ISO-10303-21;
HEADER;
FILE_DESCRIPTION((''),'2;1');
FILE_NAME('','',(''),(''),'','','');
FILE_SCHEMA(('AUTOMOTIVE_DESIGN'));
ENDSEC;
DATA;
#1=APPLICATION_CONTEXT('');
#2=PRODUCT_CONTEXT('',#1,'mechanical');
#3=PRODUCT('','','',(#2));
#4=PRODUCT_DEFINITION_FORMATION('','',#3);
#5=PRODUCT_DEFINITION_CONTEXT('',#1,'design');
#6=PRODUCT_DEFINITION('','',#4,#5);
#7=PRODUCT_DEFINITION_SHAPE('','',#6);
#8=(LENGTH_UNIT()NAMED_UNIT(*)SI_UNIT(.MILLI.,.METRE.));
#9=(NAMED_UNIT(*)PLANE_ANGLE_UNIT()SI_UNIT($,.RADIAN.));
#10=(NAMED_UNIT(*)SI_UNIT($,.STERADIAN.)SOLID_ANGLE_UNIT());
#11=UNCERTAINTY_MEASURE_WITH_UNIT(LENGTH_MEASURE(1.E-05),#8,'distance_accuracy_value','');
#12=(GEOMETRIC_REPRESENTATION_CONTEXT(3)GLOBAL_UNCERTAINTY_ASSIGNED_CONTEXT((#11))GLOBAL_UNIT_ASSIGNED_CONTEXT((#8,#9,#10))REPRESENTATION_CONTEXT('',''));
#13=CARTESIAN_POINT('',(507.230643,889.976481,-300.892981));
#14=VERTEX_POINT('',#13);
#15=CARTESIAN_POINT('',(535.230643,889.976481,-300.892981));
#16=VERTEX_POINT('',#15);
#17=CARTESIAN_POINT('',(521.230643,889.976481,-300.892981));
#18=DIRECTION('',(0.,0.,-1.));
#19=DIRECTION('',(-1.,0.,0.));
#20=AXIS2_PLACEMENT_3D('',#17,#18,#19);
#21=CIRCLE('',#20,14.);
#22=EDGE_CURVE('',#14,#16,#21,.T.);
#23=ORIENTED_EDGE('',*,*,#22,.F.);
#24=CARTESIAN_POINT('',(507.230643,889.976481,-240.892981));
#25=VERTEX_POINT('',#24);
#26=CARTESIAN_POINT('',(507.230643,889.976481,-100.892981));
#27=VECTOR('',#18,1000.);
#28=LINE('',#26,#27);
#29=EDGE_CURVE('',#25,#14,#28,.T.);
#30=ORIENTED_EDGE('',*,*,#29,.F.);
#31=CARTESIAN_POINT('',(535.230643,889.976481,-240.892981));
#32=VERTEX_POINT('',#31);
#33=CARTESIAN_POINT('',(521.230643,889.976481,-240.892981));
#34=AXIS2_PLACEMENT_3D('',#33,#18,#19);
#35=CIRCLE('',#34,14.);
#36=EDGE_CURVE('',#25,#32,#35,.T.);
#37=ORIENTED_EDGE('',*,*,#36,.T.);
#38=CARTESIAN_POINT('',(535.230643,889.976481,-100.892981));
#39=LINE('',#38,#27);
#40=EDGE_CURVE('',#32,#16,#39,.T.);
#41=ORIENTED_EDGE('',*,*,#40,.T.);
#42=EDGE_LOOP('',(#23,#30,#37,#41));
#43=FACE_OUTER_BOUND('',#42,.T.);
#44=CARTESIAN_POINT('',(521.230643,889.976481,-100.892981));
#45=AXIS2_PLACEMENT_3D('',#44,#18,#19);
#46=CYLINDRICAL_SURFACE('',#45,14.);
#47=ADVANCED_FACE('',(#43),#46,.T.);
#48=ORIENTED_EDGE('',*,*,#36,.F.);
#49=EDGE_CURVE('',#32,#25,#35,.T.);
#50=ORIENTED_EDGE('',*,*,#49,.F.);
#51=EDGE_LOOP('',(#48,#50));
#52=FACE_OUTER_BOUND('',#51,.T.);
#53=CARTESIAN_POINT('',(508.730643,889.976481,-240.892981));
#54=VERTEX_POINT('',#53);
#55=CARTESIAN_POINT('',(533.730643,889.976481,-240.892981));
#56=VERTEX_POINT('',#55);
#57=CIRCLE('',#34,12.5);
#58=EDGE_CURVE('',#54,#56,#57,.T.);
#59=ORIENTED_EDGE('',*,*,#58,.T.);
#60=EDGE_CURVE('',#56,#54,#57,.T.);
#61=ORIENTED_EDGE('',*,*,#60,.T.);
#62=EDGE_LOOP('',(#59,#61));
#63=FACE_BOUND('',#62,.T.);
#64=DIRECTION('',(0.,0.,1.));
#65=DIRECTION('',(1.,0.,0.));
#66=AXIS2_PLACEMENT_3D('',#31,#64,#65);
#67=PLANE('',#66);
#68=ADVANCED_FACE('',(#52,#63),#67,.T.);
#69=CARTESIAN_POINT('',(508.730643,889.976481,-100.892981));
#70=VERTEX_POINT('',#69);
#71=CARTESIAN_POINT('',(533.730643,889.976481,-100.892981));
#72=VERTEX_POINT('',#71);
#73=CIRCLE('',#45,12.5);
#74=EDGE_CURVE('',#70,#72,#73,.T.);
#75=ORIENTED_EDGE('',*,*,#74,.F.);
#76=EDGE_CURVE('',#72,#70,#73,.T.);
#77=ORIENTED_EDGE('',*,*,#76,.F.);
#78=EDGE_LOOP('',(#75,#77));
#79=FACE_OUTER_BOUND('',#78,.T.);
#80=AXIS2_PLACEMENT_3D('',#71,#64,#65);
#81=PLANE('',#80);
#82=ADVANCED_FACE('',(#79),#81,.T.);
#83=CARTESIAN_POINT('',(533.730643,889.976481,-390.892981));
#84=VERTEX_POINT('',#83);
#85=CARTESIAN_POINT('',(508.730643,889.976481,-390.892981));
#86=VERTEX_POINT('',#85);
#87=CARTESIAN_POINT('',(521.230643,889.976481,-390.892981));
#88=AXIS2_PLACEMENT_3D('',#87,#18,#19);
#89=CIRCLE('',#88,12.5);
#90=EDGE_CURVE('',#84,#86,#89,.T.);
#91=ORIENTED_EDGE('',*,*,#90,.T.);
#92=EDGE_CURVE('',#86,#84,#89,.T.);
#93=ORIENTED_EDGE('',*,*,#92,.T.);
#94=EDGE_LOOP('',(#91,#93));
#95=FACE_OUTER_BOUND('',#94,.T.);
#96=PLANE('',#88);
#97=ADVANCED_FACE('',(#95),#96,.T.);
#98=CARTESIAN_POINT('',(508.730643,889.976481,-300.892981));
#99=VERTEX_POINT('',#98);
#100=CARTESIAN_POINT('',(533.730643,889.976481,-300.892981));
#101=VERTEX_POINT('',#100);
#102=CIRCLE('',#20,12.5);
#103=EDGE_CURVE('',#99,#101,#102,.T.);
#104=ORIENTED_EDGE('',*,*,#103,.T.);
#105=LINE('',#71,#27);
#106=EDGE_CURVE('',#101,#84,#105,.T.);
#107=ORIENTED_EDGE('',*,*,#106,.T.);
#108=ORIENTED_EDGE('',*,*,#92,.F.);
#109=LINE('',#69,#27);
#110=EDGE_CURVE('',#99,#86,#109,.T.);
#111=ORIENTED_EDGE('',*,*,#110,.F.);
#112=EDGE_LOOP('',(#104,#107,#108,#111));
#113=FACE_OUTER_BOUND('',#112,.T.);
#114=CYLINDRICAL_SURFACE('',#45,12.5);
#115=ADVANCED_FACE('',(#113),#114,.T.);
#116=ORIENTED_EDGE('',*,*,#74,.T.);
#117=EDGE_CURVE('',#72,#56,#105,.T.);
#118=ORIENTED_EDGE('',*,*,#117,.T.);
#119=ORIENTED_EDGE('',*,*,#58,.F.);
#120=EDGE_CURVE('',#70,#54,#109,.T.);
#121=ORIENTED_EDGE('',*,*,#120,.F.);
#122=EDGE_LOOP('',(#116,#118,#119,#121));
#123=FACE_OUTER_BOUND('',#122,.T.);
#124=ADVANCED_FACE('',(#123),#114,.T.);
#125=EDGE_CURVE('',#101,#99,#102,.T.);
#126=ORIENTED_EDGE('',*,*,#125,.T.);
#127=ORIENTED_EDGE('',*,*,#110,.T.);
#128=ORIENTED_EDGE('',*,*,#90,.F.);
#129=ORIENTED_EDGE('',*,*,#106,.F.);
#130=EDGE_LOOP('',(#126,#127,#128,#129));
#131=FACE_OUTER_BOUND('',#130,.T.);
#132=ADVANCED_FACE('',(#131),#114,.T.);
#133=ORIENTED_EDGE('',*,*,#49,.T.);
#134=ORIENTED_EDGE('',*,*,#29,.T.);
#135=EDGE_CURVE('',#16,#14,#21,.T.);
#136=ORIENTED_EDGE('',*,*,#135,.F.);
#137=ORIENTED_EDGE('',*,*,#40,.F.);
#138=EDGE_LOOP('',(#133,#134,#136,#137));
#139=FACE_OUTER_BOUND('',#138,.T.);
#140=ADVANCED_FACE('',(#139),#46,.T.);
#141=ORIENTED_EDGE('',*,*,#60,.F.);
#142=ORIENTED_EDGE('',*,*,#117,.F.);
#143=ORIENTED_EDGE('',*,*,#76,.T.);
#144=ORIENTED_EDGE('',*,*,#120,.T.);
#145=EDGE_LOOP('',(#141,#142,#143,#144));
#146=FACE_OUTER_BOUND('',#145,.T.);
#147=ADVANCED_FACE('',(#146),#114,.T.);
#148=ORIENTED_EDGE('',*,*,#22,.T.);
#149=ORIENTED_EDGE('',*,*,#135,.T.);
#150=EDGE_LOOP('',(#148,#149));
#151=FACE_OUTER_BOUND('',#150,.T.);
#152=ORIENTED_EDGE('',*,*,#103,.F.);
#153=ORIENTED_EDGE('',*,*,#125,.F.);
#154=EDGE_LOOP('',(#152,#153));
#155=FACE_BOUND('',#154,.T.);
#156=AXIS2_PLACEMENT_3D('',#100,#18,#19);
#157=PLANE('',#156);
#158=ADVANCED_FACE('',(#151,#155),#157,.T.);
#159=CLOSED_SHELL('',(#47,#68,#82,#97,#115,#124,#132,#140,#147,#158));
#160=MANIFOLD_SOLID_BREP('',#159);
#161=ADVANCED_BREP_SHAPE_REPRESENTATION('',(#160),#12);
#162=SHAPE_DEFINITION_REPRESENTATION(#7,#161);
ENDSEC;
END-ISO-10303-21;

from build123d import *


with BuildPart() as part:
    # Sketch1 → Revolve1 (revolve)
    with BuildSketch(Plane.XZ.offset(-889.976481234), mode=Mode.PRIVATE) as revolve1_sk:
        Polygon((533.730642584, -100.892981355), (521.230642584, -100.892981355), (521.230642584, -390.892981355), (533.730642584, -390.892981355), (533.730642584, -300.892981355), (535.230642584, -300.892981355), (535.230642584, -240.892981355), (533.730642584, -240.892981355), align=None)
    revolve(revolve1_sk.sketch.rotate(Axis((521.230642584, 889.976481234, -100.892981355), (0, 0, -1)), 180), axis=Axis((521.230642584, 889.976481234, -100.892981355), (0, 0, -1)))


solid = part.part
